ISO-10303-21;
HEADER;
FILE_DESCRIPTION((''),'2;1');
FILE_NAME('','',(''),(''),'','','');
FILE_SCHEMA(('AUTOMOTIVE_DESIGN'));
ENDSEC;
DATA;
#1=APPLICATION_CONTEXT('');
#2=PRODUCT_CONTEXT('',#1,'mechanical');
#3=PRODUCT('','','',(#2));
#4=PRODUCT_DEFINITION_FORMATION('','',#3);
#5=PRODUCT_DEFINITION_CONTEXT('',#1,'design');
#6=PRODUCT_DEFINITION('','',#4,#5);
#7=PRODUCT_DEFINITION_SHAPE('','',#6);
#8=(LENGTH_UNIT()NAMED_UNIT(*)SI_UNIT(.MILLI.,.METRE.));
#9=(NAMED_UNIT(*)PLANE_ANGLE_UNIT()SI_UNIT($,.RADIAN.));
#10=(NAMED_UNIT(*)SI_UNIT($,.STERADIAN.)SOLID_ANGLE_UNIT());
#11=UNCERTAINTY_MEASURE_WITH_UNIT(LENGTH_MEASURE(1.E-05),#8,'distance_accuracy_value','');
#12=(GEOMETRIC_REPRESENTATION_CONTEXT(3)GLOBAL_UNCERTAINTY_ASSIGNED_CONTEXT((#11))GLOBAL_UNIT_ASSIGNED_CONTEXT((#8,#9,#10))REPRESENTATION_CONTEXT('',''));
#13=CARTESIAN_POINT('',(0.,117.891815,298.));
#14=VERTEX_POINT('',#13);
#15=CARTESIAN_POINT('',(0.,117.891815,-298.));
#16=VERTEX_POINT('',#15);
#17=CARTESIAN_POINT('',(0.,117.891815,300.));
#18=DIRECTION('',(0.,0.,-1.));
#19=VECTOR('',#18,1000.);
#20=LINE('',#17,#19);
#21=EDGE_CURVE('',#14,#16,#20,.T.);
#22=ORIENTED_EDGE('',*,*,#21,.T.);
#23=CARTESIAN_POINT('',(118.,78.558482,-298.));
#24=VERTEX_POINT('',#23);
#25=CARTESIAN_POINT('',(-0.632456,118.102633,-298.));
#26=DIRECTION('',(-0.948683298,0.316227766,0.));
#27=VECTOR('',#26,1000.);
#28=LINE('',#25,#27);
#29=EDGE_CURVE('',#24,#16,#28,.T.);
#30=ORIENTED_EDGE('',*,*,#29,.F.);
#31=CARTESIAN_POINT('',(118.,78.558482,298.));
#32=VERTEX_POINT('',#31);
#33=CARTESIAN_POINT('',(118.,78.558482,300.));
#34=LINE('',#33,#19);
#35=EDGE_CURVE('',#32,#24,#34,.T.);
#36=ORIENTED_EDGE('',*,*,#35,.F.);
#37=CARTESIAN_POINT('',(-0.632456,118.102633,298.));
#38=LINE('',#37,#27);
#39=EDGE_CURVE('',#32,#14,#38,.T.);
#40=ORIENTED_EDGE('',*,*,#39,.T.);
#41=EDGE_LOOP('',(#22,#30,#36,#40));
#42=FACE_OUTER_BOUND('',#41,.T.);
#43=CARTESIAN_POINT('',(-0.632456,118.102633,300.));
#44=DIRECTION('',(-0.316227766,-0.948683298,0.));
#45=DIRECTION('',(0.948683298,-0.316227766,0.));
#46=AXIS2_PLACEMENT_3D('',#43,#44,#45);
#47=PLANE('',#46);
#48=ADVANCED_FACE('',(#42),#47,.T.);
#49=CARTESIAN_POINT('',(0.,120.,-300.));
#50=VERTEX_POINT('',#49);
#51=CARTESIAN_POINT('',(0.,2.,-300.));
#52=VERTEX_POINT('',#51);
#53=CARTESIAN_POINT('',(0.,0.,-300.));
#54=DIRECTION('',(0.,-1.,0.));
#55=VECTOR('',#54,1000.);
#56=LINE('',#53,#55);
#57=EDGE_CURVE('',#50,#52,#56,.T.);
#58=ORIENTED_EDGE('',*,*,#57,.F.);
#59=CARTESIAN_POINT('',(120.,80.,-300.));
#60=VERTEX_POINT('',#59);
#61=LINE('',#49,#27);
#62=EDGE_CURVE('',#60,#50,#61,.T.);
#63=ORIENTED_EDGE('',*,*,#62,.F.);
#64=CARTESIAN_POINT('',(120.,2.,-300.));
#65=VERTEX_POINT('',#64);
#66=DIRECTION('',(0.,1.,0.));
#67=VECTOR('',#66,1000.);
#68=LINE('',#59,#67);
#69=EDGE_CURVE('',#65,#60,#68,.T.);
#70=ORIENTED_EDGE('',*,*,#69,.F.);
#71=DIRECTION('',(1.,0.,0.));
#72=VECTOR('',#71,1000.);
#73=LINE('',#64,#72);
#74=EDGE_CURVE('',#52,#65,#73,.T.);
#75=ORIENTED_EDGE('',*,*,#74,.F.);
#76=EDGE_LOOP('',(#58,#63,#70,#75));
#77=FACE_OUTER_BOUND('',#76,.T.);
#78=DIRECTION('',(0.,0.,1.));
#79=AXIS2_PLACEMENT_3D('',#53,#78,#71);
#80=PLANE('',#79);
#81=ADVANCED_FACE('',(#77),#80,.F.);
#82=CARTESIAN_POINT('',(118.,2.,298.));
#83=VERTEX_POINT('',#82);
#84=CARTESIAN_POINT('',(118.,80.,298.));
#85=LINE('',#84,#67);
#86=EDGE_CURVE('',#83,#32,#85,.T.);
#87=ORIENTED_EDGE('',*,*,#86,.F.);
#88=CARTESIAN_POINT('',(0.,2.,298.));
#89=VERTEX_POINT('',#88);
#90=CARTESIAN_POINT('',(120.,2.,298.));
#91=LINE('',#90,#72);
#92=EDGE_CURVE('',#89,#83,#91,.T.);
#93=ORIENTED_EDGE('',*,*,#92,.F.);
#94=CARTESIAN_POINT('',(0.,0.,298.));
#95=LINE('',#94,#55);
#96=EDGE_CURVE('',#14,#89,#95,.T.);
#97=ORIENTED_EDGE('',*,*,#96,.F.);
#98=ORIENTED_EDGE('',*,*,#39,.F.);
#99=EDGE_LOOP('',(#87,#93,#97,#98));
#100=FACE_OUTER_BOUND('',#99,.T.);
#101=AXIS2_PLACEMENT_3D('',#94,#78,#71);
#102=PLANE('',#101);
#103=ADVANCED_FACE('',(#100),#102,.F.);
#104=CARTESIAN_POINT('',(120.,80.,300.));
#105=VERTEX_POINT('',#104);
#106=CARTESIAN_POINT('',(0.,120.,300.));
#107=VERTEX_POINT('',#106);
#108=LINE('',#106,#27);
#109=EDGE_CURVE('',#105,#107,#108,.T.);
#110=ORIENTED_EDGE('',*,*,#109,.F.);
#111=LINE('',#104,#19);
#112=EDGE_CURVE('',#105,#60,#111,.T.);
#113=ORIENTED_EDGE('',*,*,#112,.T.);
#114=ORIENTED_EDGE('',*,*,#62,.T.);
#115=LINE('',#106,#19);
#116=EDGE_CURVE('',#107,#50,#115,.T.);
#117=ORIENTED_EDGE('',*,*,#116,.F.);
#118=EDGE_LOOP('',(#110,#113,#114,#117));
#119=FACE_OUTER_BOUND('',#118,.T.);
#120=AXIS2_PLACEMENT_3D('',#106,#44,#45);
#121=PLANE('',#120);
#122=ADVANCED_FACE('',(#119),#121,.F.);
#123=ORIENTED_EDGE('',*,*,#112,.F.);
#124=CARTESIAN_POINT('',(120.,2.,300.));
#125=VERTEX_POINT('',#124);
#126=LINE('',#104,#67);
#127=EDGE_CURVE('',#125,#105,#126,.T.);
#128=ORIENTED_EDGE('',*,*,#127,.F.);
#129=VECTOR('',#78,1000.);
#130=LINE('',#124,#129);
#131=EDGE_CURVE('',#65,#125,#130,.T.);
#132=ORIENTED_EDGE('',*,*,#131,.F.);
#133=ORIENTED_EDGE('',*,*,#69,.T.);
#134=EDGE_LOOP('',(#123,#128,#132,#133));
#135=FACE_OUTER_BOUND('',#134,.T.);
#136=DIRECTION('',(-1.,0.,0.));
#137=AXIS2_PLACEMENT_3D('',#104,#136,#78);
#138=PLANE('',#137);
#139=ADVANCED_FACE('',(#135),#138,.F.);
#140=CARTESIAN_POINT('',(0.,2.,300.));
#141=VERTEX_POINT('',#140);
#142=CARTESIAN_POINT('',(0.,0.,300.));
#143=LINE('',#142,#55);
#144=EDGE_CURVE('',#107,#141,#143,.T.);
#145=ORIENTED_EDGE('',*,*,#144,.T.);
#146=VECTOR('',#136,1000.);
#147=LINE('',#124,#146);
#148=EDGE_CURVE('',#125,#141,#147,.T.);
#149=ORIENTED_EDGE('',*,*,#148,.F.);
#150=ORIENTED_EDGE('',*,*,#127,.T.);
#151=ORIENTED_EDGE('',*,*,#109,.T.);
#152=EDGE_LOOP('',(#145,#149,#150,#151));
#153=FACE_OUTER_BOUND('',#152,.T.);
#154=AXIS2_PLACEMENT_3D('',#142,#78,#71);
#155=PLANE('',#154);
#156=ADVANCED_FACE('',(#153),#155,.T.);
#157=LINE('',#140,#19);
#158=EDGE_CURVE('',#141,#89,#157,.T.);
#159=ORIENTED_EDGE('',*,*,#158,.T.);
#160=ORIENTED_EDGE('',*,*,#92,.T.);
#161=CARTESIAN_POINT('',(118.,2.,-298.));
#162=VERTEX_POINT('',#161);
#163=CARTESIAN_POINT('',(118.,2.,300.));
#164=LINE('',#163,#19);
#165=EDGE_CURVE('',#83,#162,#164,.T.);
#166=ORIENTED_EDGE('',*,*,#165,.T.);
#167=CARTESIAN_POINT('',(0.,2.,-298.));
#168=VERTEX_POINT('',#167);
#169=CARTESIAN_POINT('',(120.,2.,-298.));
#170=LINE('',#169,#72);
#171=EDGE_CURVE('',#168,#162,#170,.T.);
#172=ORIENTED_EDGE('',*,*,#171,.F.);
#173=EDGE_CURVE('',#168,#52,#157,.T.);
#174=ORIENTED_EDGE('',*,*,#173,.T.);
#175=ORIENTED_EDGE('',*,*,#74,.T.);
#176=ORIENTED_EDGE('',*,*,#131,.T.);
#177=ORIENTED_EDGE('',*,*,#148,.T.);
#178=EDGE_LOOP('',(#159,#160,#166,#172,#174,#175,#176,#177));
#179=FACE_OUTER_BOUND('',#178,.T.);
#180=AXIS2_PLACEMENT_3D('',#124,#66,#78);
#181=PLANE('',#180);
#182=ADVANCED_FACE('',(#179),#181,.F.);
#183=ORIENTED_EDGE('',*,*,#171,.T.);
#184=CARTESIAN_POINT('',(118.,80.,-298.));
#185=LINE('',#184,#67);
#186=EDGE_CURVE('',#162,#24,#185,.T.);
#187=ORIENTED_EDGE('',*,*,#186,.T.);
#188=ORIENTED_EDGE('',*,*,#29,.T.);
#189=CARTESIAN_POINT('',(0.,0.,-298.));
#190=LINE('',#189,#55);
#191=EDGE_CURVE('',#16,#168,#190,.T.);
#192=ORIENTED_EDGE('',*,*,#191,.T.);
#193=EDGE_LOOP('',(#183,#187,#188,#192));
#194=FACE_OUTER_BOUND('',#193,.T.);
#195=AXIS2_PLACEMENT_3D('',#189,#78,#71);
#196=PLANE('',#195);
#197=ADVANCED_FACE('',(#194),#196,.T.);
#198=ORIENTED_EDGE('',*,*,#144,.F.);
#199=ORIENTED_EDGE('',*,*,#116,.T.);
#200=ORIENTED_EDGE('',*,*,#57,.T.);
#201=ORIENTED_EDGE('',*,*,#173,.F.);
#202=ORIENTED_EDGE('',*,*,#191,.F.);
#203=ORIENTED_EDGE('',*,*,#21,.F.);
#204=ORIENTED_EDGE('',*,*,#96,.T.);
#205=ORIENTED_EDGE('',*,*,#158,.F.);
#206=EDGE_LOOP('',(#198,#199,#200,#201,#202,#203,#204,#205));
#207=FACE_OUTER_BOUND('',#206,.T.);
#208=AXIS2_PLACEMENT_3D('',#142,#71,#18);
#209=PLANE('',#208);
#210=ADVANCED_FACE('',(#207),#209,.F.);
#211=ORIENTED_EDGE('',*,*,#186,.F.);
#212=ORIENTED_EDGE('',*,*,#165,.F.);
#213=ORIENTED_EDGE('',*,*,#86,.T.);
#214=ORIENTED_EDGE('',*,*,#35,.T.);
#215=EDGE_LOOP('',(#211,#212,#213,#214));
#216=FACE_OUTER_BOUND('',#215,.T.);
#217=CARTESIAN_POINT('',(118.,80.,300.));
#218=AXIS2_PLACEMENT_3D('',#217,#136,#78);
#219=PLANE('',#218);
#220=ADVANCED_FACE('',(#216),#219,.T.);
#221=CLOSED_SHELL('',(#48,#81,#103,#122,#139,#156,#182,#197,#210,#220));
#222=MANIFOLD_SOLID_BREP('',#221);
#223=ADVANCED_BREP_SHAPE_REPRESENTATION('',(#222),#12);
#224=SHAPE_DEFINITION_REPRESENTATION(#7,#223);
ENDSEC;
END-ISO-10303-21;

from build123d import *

# Parameters (mm, degrees)
BOSS_EXTRUDE1_DEPTH = 300
SHELL1_T            = -2
SKETCH2_W           = 120
SKETCH2_H           = 600
CUT_EXTRUDE1_DEPTH  = 2


with BuildPart() as part:
    # Sketch1 → Boss-Extrude1 (new, symmetric)
    with BuildSketch(Plane.XY):
        Polygon((0, 120), (120, 80), (120, 0), (0, 0), align=None)
    extrude(amount=BOSS_EXTRUDE1_DEPTH, both=True)

    # Shell1
    shell1_openings = [part.faces().sort_by_distance(p)[0] for p in [
        (0, 60, 0),
    ]]
    offset(amount=SHELL1_T, openings=shell1_openings, kind=Kind.INTERSECTION)

    # Sketch2 → Cut-Extrude1 (cut)
    with BuildSketch(Plane.XZ):
        with Locations((60, 0)):
            Rectangle(SKETCH2_W, SKETCH2_H)
    extrude(amount=-CUT_EXTRUDE1_DEPTH, mode=Mode.SUBTRACT)


solid = part.part
